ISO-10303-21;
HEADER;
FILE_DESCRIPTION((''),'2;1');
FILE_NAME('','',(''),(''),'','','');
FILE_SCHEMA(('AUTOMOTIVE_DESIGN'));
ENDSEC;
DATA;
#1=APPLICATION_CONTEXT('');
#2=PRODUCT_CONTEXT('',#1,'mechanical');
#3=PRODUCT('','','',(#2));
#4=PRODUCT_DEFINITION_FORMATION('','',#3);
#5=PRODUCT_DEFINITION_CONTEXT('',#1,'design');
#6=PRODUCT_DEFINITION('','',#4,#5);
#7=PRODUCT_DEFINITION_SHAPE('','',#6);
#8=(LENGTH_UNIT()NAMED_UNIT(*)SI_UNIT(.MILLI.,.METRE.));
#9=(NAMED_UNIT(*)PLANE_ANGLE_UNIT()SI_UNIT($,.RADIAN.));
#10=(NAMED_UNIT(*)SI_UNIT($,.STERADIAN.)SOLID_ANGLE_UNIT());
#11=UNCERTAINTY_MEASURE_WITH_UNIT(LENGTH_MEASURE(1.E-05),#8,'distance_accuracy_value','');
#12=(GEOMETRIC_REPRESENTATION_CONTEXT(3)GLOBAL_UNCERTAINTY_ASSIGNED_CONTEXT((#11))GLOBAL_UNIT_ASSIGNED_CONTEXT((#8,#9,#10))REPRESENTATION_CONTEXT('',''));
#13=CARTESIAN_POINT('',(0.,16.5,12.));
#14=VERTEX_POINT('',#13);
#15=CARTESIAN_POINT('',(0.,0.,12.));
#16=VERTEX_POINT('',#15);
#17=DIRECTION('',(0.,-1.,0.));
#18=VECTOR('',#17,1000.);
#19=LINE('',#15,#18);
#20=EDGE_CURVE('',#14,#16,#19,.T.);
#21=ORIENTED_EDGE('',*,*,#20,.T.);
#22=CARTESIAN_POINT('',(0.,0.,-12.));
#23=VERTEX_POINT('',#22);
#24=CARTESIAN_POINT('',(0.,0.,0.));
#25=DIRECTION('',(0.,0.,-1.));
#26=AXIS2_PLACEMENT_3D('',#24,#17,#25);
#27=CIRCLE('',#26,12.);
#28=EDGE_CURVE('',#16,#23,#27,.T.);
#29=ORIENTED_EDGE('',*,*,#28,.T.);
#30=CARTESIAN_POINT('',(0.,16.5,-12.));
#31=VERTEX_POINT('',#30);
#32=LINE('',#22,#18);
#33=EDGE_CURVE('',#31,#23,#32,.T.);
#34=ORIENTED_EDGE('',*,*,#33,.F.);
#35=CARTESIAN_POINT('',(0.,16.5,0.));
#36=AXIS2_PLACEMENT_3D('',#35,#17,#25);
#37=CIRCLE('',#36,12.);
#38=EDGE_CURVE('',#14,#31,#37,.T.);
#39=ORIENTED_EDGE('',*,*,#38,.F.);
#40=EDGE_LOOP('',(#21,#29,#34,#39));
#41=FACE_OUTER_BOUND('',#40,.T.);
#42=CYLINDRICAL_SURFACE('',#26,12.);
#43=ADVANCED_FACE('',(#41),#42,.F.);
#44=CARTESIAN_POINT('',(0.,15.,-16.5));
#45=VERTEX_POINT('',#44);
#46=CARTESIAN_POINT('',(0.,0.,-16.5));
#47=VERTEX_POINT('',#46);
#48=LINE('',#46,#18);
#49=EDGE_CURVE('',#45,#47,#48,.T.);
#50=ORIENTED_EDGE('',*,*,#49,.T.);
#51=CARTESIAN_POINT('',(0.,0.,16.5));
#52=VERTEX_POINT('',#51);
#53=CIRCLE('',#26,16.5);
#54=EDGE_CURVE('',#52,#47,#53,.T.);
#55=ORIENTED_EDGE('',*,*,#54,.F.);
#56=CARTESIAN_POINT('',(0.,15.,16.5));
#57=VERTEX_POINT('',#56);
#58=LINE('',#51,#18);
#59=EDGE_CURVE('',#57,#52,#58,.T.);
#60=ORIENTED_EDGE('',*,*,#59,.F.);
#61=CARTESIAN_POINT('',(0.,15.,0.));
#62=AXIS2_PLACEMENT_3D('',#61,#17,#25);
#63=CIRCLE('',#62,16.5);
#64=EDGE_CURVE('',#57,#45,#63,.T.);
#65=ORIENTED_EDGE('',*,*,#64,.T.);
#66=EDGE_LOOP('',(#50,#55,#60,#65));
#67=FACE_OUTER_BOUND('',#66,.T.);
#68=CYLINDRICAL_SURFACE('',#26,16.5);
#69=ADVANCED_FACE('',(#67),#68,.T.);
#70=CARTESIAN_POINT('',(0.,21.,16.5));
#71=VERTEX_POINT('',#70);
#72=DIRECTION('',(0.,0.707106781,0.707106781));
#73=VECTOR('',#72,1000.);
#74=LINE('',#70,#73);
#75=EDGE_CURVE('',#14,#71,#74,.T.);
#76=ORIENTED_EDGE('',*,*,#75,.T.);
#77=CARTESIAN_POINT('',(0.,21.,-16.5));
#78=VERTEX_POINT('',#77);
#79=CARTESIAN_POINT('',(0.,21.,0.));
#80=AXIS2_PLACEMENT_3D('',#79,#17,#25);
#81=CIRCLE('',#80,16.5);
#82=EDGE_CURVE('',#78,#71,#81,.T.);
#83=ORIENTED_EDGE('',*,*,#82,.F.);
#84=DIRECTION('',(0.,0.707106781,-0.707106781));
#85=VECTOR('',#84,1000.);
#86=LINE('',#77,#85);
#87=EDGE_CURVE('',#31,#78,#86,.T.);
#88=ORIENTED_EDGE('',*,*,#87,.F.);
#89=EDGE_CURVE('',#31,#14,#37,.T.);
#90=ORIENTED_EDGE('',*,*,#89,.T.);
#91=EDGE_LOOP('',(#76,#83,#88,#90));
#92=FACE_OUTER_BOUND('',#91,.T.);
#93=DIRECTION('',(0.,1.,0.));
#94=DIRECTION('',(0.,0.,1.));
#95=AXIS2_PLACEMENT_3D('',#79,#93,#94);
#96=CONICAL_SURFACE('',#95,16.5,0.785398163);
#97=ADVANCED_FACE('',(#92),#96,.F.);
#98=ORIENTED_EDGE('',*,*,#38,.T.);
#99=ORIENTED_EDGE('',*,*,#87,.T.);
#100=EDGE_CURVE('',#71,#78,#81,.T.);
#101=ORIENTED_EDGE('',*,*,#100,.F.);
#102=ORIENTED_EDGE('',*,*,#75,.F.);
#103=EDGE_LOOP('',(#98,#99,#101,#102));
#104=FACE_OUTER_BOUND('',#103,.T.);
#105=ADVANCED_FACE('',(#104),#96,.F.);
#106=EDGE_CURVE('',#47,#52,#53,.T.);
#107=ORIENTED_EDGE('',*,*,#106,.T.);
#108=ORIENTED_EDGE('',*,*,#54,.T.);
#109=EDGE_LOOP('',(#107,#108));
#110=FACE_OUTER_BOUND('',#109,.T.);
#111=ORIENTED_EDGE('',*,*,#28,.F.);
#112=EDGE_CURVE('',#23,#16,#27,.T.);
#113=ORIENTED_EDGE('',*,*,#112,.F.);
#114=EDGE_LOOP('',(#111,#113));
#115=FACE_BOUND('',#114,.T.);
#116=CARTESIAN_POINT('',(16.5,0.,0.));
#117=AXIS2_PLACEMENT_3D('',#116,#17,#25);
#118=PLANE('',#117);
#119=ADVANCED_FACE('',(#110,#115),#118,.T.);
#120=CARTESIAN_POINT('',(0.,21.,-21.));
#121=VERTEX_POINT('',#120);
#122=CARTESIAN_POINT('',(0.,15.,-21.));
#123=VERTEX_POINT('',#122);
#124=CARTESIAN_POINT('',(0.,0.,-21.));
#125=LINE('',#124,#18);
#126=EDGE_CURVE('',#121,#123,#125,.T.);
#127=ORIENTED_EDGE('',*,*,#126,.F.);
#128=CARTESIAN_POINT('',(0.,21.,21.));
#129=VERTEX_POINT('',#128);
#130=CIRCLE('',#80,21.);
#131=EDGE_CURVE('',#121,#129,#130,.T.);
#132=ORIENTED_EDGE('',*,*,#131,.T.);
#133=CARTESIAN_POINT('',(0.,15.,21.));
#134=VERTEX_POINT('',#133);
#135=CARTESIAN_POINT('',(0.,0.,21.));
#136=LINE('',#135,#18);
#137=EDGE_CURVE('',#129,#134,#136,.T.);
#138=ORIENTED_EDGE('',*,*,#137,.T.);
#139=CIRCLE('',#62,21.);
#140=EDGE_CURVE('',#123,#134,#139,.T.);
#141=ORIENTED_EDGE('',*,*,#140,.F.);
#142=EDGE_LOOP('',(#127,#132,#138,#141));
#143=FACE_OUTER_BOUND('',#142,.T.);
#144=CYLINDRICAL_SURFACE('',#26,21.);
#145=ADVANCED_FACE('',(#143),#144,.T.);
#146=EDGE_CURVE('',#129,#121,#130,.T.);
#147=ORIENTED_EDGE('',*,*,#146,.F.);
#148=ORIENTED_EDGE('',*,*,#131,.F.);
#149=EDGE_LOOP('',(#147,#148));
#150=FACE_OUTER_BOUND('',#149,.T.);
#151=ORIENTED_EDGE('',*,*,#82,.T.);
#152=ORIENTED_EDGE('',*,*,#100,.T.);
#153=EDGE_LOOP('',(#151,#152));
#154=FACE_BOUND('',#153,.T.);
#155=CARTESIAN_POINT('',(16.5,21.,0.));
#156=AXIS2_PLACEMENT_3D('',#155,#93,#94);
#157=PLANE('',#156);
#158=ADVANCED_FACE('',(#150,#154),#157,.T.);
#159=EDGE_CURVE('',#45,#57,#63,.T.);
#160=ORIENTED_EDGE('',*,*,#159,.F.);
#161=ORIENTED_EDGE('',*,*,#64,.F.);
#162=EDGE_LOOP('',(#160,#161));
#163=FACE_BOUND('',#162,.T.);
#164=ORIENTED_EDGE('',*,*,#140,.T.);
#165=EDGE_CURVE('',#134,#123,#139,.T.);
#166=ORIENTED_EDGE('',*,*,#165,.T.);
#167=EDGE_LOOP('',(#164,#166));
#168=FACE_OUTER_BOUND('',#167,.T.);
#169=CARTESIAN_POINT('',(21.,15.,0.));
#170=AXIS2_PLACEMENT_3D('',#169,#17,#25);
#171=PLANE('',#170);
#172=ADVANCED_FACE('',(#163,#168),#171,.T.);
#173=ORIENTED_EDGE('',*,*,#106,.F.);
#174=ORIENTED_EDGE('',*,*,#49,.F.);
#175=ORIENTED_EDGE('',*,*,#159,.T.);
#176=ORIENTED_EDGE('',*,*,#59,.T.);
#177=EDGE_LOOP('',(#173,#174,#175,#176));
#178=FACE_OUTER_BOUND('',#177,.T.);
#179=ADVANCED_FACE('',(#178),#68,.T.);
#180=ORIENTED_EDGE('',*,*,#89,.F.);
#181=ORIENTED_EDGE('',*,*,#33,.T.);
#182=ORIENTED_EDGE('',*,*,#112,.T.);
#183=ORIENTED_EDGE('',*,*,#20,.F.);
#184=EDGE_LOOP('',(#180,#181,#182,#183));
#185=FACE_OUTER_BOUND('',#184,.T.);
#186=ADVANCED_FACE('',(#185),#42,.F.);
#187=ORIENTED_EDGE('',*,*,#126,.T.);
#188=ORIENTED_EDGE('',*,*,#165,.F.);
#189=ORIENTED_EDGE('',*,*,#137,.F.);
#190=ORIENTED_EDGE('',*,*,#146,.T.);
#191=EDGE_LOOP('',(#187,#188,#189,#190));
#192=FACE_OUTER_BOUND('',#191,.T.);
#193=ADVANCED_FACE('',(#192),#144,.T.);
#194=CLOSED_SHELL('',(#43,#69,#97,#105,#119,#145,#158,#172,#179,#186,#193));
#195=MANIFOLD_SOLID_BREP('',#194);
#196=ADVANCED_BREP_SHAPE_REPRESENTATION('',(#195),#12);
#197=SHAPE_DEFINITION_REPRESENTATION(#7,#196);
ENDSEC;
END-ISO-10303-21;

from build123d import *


with BuildPart() as part:
    # Bush Half-Section Profile → Flanged Bush Body (revolve)
    with BuildSketch(Plane.XY, mode=Mode.PRIVATE) as flanged_bush_body_sk:
        Polygon((12, 0), (12, 16.5), (16.5, 21), (21, 21), (21, 15), (16.5, 15), (16.5, 0), align=None)
    revolve(flanged_bush_body_sk.sketch.rotate(Axis((0, 0, 0), (0, 1, 0)), 90), axis=Axis((0, 0, 0), (0, 1, 0)))


solid = part.part
